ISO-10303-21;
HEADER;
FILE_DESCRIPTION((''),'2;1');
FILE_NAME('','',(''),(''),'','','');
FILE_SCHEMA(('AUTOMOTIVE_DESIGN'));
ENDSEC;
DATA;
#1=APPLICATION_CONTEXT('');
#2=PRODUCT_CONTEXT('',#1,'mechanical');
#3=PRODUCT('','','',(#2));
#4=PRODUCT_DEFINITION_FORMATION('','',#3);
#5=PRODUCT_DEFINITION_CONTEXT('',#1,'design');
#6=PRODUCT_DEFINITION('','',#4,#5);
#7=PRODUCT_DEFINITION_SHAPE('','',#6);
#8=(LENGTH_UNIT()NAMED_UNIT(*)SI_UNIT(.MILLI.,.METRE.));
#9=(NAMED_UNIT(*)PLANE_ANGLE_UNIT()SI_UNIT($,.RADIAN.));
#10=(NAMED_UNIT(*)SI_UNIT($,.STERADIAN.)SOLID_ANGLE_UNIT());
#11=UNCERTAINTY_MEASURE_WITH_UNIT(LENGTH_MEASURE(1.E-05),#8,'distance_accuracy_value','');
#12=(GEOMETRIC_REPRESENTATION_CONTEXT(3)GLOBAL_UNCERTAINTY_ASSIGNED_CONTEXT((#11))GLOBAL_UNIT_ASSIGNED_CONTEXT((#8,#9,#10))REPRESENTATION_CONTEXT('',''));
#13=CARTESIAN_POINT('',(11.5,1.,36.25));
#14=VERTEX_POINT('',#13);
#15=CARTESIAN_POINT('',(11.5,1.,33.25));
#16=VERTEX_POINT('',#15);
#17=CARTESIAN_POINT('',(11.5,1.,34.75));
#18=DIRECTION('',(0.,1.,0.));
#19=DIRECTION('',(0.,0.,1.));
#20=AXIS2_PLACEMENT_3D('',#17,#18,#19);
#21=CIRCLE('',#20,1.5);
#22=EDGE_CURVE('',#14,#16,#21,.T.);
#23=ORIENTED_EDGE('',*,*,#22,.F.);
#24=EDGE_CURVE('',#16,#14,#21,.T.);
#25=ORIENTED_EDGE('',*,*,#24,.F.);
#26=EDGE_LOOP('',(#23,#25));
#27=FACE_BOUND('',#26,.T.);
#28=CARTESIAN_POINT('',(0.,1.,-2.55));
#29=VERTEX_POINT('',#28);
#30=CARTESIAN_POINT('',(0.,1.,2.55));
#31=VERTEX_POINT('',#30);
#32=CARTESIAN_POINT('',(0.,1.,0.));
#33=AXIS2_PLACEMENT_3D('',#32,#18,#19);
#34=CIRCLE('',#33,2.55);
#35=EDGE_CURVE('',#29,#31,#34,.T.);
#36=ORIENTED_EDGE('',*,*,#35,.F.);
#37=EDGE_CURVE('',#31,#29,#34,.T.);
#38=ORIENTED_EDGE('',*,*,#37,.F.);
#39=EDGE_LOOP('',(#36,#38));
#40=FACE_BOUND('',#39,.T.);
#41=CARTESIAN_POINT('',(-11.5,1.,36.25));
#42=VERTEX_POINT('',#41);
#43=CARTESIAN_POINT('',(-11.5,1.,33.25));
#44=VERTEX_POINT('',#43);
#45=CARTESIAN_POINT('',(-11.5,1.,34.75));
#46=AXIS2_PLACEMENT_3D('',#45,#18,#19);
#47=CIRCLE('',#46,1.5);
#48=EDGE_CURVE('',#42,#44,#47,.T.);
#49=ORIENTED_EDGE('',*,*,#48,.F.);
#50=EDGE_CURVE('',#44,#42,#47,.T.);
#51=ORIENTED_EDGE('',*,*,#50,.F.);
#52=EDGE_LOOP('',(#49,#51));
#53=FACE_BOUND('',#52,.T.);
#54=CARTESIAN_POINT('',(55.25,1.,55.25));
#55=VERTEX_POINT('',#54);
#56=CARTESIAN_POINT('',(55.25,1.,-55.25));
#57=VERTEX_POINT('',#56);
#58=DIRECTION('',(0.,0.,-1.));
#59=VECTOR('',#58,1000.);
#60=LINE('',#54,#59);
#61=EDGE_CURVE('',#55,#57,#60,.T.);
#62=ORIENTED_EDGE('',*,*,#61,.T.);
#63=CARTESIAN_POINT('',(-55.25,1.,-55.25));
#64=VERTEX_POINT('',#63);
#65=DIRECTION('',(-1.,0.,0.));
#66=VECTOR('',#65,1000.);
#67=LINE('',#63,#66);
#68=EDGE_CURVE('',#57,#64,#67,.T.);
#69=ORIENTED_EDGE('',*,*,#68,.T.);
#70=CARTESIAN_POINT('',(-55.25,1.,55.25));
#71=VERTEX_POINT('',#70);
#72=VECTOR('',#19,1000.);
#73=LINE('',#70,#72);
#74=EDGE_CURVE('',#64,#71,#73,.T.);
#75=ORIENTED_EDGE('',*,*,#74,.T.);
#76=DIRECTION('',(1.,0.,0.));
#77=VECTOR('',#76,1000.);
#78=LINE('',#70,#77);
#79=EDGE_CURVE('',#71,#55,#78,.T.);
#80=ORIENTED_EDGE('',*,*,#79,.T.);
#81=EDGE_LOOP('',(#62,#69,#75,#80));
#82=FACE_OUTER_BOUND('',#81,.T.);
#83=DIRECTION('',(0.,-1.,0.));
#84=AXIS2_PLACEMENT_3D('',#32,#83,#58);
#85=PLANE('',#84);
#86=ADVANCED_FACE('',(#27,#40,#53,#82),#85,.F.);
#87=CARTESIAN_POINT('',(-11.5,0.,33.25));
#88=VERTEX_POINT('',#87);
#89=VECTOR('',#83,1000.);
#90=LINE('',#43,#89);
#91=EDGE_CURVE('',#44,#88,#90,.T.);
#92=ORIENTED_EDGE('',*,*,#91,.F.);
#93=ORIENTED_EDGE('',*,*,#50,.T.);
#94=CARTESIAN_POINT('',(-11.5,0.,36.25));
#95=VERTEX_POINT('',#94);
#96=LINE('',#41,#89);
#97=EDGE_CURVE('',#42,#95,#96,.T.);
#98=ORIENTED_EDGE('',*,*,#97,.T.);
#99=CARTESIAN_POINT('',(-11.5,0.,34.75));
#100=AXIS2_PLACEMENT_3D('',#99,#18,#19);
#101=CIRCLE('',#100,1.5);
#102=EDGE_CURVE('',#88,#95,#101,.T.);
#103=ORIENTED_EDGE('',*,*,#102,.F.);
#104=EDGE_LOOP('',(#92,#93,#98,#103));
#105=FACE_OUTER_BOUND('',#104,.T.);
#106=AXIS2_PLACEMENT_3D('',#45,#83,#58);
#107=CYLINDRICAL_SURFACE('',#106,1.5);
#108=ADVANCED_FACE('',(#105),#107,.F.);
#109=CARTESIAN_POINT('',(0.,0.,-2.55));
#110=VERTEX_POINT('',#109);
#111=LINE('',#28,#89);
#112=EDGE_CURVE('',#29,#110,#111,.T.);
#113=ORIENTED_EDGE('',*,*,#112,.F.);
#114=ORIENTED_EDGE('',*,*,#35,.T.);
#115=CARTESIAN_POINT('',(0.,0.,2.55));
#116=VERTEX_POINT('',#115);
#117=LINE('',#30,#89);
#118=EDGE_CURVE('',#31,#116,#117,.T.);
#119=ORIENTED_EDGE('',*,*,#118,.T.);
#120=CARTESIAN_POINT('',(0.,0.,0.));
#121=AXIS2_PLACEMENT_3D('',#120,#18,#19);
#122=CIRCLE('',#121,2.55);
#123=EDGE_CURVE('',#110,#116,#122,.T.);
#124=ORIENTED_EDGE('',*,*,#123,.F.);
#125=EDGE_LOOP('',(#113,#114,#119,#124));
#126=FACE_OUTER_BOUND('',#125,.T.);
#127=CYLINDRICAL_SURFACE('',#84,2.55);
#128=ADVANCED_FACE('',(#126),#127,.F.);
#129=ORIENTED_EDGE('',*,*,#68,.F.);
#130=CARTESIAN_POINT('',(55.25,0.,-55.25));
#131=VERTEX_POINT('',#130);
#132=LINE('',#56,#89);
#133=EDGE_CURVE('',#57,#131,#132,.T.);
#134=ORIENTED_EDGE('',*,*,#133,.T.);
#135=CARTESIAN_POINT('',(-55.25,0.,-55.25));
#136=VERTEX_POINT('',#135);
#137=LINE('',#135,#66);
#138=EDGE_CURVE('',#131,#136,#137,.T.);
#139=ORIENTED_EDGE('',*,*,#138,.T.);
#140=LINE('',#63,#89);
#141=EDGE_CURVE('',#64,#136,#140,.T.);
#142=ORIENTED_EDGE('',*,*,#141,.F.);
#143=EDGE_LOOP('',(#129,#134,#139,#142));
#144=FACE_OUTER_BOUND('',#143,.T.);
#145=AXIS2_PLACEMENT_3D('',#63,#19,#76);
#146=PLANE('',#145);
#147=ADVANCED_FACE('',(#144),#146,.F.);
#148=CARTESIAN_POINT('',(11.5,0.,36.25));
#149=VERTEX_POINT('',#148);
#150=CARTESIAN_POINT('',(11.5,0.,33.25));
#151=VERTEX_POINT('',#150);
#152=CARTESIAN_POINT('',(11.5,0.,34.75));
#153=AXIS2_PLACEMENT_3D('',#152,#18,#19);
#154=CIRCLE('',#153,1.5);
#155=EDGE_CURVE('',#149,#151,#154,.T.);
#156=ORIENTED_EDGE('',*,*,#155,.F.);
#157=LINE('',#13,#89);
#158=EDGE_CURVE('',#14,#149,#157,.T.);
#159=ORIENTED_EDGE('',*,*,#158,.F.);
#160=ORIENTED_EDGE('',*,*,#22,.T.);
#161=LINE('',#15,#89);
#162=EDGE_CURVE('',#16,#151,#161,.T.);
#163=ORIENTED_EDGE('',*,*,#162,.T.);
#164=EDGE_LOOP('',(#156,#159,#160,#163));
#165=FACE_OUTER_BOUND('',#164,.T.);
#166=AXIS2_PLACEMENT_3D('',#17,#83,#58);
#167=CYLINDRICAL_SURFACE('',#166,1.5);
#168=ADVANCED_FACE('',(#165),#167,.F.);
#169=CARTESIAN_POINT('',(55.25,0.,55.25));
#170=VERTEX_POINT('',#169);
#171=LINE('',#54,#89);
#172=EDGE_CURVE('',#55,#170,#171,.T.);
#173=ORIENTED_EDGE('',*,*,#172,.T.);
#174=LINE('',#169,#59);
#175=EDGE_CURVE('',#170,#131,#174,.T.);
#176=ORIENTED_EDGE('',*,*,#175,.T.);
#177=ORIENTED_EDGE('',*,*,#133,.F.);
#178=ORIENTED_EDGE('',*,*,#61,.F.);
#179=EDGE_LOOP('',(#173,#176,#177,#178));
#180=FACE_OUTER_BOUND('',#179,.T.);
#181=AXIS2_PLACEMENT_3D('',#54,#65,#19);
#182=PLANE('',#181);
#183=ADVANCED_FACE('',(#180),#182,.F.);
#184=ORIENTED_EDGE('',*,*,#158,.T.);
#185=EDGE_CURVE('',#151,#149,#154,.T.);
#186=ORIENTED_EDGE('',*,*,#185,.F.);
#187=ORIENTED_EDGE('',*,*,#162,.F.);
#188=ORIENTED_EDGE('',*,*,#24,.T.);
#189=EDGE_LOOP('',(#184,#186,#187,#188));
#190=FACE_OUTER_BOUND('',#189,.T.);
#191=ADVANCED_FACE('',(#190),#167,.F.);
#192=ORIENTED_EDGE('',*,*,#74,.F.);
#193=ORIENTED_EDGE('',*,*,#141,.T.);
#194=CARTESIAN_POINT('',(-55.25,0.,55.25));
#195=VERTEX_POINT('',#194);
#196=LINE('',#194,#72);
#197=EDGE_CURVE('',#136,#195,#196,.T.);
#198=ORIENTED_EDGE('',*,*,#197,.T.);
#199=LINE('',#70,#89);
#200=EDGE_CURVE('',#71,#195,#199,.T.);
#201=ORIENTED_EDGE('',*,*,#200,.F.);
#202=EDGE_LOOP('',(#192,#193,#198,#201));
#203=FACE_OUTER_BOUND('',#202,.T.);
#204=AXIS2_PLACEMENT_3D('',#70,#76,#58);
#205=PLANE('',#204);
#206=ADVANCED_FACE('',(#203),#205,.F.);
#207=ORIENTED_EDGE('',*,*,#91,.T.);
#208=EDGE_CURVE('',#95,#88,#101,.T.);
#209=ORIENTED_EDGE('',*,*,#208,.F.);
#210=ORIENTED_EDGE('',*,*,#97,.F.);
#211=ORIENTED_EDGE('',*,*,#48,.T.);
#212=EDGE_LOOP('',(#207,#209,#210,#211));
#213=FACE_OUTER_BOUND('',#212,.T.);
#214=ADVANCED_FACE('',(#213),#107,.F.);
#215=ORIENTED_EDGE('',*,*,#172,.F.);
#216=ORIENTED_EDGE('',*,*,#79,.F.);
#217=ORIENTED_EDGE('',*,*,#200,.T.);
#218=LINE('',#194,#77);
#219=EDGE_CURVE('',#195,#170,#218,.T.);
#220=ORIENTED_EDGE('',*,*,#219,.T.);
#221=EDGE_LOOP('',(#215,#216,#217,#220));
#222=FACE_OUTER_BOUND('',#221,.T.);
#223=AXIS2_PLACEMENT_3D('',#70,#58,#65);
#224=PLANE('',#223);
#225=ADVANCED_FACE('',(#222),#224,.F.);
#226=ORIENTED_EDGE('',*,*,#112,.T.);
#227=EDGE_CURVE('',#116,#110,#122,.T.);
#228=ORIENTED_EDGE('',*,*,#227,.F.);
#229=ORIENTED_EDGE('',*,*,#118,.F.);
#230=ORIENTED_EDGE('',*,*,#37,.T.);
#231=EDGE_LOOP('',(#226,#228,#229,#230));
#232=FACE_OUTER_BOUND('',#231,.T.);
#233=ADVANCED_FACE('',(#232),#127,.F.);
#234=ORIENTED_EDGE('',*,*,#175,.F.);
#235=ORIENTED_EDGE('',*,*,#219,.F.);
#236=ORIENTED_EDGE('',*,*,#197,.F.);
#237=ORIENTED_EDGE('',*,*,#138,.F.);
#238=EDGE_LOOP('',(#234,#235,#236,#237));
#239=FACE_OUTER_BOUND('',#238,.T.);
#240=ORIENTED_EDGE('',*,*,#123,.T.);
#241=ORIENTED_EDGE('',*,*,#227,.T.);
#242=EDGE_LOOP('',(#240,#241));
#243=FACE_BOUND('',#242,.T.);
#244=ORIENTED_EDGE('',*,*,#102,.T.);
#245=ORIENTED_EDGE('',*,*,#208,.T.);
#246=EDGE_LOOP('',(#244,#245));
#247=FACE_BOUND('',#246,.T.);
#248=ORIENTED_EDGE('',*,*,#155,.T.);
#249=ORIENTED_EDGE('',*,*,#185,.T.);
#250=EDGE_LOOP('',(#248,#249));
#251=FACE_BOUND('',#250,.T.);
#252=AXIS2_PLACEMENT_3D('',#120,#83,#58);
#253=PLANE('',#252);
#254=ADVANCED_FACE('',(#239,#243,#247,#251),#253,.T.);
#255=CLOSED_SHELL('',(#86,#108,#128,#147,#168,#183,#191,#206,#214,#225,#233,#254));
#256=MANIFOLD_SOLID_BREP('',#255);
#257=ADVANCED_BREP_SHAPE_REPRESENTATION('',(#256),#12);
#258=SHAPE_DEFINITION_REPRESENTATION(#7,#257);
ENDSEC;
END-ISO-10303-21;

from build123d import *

# Parameters (mm, degrees)
SKETCH1_W           = 110.5
SKETCH1_H           = 110.5
SKETCH1_R           = 2.55
SKETCH1_R_2         = 1.5
BOSS_EXTRUDE1_DEPTH = 1


with BuildPart() as part:
    # Sketch1 → Boss-Extrude1 (new body)
    with BuildSketch(Plane(origin=(0, 0, 0), x_dir=(1, 0, 0), z_dir=(0, 1, 0))):
        Rectangle(SKETCH1_W, SKETCH1_H)
        with Locations(Location((0, 0, 0), (0, 0, 270))):
            Circle(SKETCH1_R, mode=Mode.SUBTRACT)
        with Locations(Location((-11.5, -34.75, 0), (0, 0, 270))):
            Circle(SKETCH1_R_2, mode=Mode.SUBTRACT)
        with Locations(Location((11.5, -34.75, 0), (0, 0, 270))):
            Circle(SKETCH1_R_2, mode=Mode.SUBTRACT)
    extrude(amount=BOSS_EXTRUDE1_DEPTH)


solid = part.part
